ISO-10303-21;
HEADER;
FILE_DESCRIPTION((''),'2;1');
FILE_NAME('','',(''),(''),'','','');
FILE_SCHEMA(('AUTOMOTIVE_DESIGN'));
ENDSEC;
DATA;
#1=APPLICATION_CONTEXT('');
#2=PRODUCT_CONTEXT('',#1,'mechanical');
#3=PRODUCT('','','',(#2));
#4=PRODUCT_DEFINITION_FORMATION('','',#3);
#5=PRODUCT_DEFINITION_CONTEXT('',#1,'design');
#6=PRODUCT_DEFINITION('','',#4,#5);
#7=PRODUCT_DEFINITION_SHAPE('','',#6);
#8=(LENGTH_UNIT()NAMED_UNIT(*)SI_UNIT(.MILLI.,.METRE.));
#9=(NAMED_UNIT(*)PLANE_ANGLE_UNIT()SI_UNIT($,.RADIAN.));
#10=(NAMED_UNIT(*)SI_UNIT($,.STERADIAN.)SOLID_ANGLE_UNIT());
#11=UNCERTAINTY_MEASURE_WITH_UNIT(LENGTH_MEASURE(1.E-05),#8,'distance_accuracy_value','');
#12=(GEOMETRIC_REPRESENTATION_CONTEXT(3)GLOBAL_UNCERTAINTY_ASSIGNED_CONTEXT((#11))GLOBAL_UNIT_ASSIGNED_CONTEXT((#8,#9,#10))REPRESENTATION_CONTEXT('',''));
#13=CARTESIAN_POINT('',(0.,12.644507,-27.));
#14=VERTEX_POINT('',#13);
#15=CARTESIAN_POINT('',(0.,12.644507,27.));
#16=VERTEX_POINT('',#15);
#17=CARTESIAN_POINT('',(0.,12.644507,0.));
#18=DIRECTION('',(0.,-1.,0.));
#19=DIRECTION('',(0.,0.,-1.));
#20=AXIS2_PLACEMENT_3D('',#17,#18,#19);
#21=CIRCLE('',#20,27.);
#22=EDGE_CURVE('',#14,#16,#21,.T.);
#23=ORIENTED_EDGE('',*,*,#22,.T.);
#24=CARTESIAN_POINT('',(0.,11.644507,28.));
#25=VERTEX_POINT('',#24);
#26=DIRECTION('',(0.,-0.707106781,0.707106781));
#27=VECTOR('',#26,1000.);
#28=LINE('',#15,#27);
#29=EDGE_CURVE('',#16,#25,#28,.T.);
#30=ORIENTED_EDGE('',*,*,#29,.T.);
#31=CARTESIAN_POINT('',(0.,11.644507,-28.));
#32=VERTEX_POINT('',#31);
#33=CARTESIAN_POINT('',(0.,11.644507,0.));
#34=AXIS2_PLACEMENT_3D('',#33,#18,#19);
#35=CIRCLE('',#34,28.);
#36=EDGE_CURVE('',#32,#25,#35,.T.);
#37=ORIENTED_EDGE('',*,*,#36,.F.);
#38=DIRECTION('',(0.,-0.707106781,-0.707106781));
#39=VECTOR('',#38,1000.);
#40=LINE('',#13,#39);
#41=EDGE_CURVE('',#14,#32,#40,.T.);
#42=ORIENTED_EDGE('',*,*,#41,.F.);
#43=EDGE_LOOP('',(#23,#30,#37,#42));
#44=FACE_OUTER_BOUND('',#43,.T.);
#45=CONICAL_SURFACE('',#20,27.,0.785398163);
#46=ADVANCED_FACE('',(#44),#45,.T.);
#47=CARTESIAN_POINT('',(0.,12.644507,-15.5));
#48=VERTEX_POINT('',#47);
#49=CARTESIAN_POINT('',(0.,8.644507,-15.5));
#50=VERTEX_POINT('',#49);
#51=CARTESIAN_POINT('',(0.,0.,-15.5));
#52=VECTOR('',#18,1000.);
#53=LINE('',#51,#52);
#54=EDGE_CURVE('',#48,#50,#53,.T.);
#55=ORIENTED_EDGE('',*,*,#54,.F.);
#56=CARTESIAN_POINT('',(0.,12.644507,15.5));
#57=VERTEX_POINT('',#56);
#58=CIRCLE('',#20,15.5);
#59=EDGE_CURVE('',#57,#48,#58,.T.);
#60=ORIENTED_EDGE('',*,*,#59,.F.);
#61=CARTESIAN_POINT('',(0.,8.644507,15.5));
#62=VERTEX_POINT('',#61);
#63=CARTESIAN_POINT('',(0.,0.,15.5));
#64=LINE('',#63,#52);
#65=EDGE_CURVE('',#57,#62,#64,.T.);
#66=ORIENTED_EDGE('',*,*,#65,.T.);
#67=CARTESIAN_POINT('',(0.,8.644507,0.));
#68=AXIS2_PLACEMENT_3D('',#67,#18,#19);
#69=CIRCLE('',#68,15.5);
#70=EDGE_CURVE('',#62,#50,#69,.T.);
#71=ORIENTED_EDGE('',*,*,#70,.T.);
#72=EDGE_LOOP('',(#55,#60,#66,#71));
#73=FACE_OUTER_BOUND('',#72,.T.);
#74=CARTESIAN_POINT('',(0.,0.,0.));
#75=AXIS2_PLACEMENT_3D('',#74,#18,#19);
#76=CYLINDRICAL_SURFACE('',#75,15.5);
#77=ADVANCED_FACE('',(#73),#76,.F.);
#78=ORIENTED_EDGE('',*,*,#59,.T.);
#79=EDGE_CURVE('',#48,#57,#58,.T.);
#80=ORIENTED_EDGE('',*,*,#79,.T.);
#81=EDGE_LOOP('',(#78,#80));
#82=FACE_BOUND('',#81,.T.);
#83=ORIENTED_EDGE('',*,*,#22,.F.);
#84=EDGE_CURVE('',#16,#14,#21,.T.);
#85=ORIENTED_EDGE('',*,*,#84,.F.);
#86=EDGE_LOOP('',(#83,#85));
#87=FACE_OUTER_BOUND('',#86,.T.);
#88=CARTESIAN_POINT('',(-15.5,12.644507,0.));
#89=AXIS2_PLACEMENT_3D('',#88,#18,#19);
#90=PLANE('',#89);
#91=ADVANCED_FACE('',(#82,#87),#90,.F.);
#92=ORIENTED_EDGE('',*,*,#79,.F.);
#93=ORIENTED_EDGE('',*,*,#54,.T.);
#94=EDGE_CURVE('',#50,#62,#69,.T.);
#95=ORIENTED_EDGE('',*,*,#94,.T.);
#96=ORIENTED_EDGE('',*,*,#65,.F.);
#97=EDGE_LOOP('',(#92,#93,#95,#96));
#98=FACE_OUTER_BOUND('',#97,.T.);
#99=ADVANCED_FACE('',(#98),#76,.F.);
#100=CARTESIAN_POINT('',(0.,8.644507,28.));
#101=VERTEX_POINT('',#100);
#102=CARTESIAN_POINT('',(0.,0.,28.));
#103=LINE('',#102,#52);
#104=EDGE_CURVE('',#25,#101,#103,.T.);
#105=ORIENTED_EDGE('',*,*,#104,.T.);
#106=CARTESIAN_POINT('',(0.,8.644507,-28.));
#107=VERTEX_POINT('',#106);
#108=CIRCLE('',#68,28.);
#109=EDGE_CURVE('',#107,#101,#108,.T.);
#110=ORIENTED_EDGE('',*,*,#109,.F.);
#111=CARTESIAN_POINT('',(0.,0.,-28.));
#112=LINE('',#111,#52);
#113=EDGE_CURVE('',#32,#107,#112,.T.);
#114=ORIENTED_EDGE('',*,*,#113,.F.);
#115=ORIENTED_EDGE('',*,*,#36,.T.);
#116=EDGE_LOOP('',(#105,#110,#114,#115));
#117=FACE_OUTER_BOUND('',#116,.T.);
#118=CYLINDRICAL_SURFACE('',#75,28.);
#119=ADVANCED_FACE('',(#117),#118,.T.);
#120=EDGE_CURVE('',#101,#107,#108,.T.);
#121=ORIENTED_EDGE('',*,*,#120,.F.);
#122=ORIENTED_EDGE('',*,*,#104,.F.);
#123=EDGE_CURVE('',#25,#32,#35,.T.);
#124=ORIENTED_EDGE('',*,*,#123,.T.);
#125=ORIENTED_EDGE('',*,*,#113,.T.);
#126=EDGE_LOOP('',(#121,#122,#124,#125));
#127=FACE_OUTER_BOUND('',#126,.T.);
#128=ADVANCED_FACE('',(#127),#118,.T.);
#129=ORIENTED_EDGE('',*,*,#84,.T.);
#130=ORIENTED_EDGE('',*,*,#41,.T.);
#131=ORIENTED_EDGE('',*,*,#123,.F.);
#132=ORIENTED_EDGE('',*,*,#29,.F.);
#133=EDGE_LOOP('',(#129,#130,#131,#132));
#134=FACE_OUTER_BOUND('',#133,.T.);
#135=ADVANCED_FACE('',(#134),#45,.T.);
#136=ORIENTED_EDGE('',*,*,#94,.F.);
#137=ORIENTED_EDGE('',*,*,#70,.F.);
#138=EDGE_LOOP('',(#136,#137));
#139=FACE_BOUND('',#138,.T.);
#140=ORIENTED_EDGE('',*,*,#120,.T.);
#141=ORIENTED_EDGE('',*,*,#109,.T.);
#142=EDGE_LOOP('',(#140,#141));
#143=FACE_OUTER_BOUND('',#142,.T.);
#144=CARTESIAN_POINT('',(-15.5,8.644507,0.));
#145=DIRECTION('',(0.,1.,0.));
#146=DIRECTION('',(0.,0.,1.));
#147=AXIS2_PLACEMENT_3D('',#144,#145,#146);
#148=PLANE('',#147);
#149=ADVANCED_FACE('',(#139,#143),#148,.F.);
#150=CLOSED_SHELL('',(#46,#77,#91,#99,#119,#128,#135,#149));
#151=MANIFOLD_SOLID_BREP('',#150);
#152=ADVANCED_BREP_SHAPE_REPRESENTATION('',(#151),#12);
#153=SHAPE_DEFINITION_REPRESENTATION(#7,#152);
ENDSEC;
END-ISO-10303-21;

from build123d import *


with BuildPart() as part:
    # 草图1 → Revolve 481 (revolve)
    with BuildSketch(Plane.XY, mode=Mode.PRIVATE) as revolve_481_sk:
        Polygon((-27, 12.644507042), (-28, 11.644507042), (-28, 8.644507042), (-15.5, 8.644507042), (-15.5, 12.644507042), align=None)
    revolve(revolve_481_sk.sketch.rotate(Axis((0, 0, 0), (0, 1, 0)), 270), axis=Axis((0, 0, 0), (0, 1, 0)))


solid = part.part
